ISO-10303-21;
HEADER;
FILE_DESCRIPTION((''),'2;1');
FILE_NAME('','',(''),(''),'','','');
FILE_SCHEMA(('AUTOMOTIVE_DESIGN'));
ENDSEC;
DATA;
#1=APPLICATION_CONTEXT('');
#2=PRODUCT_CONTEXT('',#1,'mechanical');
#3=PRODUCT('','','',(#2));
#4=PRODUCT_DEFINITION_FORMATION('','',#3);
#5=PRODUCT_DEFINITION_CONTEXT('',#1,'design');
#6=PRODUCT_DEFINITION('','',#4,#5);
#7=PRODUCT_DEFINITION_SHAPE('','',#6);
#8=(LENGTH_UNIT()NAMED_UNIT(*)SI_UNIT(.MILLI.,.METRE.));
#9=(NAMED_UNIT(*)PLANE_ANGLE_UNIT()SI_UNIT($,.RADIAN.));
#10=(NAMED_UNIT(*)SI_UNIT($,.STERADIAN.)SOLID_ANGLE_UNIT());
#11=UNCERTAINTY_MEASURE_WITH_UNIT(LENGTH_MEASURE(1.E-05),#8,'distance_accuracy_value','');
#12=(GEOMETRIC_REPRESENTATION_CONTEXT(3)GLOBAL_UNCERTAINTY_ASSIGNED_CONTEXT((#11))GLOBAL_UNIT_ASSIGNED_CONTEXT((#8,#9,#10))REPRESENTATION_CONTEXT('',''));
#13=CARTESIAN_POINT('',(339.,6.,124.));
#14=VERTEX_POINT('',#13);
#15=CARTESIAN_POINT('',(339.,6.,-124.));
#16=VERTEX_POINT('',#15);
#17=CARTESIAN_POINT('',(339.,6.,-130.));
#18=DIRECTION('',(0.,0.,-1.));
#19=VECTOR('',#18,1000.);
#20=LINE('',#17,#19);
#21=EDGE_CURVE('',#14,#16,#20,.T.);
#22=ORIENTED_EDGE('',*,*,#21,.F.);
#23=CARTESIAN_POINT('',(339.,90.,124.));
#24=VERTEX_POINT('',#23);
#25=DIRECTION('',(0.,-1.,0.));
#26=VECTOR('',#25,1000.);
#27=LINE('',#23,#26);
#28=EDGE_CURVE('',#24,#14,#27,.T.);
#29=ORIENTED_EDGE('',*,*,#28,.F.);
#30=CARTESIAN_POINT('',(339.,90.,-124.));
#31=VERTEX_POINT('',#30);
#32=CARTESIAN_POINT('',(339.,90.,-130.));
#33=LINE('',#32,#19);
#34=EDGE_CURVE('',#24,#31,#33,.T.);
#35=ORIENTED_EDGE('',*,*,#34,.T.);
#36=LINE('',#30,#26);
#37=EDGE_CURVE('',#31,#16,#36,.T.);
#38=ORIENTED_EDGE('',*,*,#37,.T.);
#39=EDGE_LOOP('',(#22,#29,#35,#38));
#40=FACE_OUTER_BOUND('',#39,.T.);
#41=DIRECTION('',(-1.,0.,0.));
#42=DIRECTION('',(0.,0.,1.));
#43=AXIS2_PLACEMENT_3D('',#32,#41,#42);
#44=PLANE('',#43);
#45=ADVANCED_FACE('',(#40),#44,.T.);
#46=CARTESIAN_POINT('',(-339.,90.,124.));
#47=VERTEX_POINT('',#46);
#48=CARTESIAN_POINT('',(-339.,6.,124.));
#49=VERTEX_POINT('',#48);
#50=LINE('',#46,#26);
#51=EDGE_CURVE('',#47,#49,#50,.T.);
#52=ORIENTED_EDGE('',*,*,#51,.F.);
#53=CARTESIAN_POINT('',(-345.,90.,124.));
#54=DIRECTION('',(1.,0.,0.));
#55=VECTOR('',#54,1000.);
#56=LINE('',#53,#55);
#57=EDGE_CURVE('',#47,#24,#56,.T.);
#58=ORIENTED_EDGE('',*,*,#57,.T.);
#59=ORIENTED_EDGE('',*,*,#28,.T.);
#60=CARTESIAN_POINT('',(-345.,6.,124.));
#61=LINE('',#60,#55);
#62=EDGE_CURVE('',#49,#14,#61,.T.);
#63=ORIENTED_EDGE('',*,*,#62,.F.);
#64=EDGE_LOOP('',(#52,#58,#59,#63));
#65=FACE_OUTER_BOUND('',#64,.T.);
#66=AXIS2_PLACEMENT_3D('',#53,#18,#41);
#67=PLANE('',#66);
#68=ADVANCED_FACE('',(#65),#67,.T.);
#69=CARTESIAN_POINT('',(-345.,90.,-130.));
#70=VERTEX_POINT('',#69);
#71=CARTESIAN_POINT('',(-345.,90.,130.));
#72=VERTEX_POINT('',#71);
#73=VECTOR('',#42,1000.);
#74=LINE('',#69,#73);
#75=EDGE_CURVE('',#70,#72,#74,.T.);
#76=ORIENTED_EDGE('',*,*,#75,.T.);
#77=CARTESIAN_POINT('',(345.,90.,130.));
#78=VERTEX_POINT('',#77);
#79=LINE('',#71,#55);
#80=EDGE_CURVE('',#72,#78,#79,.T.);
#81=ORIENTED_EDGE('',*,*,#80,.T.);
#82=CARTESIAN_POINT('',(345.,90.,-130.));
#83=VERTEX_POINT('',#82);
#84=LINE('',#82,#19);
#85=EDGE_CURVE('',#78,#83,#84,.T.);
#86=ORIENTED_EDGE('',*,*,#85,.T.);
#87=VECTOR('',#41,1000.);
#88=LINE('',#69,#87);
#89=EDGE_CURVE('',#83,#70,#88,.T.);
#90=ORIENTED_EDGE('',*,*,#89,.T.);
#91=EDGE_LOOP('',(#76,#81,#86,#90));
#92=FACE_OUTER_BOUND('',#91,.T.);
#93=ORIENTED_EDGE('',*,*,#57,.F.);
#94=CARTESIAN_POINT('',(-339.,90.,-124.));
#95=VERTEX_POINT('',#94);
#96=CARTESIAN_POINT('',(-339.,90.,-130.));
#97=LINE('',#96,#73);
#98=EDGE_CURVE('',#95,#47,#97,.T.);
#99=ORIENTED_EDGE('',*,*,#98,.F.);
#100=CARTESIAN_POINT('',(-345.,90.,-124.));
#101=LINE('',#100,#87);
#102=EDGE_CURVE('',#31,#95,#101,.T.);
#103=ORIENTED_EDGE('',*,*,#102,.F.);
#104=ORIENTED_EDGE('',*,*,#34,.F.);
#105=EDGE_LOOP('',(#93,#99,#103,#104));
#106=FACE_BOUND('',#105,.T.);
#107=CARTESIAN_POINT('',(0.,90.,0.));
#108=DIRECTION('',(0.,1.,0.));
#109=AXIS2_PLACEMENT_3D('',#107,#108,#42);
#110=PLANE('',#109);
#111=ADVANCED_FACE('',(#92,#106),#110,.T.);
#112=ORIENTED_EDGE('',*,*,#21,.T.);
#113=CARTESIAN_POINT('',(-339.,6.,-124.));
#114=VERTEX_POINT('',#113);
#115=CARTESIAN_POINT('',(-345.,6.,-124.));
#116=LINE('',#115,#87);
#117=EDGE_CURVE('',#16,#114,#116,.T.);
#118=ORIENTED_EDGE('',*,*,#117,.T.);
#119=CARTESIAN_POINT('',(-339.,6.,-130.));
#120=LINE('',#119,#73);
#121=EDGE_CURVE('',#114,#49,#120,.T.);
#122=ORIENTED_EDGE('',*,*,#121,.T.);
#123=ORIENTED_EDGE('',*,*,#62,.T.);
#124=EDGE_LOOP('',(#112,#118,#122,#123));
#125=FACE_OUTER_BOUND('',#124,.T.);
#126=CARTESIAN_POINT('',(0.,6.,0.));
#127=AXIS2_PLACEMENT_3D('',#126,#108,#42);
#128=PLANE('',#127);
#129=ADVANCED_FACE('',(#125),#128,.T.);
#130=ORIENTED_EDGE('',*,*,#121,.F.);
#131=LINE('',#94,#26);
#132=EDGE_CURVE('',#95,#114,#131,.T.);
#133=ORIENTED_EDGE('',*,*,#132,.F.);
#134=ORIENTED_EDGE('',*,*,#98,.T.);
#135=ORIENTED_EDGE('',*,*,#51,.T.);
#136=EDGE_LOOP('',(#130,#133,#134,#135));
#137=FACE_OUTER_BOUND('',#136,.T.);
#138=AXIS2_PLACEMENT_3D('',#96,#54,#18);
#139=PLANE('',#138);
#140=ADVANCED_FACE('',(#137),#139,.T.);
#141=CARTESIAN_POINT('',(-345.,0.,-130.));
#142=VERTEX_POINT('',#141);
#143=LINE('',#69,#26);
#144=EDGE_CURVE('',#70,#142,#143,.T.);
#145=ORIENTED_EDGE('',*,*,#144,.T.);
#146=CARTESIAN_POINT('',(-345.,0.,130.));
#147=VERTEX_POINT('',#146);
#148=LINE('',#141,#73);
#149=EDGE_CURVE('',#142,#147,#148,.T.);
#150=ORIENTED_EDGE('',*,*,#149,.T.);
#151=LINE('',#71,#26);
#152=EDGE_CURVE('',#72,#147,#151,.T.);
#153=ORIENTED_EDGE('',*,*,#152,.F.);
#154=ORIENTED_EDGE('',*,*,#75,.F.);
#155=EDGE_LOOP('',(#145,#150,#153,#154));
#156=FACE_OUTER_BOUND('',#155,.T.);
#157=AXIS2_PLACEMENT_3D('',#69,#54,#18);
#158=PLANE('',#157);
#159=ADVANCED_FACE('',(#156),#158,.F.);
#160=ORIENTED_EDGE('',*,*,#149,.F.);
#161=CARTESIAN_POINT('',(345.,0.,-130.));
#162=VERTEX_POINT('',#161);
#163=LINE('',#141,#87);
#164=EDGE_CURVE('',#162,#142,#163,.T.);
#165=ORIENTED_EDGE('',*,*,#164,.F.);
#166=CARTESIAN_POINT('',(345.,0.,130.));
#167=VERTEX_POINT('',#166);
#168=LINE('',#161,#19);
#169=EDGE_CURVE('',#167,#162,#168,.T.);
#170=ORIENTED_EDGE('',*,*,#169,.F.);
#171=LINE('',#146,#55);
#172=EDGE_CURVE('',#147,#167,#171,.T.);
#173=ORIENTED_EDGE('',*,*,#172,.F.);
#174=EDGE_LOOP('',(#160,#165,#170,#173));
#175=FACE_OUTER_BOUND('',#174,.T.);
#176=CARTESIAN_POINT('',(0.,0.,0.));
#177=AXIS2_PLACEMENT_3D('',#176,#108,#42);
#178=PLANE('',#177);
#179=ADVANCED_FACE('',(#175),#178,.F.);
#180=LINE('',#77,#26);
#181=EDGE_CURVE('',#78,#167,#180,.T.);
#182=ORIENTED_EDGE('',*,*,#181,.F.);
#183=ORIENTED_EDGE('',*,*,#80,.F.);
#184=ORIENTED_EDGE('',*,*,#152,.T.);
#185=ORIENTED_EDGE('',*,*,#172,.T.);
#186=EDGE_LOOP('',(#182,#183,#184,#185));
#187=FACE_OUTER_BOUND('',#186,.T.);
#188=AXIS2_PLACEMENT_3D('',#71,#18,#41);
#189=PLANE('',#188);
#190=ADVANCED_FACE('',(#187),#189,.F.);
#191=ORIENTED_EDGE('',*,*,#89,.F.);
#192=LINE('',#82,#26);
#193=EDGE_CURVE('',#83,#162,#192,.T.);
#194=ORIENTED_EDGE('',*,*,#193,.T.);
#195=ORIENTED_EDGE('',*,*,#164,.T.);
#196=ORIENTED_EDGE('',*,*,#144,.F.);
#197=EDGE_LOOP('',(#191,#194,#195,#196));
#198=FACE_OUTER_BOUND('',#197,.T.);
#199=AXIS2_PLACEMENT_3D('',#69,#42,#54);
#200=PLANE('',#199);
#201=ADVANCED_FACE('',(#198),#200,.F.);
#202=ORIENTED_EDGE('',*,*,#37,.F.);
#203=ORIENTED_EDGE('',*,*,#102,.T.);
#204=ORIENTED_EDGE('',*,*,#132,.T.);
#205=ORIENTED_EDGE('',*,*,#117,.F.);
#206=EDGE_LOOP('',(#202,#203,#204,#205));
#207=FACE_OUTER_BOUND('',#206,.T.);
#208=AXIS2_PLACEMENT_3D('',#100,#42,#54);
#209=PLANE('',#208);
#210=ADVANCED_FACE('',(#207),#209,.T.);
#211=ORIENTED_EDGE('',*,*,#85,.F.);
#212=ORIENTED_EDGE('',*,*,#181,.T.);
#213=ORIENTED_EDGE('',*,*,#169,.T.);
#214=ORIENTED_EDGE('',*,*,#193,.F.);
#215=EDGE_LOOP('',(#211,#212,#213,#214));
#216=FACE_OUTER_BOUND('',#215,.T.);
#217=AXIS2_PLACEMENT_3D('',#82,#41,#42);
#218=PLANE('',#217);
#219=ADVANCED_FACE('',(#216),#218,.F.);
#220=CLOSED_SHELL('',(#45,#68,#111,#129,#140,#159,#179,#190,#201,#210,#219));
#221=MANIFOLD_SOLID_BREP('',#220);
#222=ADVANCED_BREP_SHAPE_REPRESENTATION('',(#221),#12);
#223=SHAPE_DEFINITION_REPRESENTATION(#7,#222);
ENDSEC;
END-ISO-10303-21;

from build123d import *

# Parameters (mm, degrees)
SKETCH1_W           = 690
SKETCH1_H           = 260
BOSS_EXTRUDE1_DEPTH = 90
SHELL1_T            = -6


with BuildPart() as part:
    # Sketch1 → Boss-Extrude1 (new body)
    with BuildSketch(Plane(origin=(0, 0, 0), x_dir=(1, 0, 0), z_dir=(0, 1, 0))):
        Rectangle(SKETCH1_W, SKETCH1_H)
    extrude(amount=BOSS_EXTRUDE1_DEPTH)

    # Shell1
    shell1_openings = [part.faces().sort_by_distance(p)[0] for p in [
        (0, 90, 0),
    ]]
    offset(amount=SHELL1_T, openings=shell1_openings, kind=Kind.INTERSECTION)


solid = part.part
